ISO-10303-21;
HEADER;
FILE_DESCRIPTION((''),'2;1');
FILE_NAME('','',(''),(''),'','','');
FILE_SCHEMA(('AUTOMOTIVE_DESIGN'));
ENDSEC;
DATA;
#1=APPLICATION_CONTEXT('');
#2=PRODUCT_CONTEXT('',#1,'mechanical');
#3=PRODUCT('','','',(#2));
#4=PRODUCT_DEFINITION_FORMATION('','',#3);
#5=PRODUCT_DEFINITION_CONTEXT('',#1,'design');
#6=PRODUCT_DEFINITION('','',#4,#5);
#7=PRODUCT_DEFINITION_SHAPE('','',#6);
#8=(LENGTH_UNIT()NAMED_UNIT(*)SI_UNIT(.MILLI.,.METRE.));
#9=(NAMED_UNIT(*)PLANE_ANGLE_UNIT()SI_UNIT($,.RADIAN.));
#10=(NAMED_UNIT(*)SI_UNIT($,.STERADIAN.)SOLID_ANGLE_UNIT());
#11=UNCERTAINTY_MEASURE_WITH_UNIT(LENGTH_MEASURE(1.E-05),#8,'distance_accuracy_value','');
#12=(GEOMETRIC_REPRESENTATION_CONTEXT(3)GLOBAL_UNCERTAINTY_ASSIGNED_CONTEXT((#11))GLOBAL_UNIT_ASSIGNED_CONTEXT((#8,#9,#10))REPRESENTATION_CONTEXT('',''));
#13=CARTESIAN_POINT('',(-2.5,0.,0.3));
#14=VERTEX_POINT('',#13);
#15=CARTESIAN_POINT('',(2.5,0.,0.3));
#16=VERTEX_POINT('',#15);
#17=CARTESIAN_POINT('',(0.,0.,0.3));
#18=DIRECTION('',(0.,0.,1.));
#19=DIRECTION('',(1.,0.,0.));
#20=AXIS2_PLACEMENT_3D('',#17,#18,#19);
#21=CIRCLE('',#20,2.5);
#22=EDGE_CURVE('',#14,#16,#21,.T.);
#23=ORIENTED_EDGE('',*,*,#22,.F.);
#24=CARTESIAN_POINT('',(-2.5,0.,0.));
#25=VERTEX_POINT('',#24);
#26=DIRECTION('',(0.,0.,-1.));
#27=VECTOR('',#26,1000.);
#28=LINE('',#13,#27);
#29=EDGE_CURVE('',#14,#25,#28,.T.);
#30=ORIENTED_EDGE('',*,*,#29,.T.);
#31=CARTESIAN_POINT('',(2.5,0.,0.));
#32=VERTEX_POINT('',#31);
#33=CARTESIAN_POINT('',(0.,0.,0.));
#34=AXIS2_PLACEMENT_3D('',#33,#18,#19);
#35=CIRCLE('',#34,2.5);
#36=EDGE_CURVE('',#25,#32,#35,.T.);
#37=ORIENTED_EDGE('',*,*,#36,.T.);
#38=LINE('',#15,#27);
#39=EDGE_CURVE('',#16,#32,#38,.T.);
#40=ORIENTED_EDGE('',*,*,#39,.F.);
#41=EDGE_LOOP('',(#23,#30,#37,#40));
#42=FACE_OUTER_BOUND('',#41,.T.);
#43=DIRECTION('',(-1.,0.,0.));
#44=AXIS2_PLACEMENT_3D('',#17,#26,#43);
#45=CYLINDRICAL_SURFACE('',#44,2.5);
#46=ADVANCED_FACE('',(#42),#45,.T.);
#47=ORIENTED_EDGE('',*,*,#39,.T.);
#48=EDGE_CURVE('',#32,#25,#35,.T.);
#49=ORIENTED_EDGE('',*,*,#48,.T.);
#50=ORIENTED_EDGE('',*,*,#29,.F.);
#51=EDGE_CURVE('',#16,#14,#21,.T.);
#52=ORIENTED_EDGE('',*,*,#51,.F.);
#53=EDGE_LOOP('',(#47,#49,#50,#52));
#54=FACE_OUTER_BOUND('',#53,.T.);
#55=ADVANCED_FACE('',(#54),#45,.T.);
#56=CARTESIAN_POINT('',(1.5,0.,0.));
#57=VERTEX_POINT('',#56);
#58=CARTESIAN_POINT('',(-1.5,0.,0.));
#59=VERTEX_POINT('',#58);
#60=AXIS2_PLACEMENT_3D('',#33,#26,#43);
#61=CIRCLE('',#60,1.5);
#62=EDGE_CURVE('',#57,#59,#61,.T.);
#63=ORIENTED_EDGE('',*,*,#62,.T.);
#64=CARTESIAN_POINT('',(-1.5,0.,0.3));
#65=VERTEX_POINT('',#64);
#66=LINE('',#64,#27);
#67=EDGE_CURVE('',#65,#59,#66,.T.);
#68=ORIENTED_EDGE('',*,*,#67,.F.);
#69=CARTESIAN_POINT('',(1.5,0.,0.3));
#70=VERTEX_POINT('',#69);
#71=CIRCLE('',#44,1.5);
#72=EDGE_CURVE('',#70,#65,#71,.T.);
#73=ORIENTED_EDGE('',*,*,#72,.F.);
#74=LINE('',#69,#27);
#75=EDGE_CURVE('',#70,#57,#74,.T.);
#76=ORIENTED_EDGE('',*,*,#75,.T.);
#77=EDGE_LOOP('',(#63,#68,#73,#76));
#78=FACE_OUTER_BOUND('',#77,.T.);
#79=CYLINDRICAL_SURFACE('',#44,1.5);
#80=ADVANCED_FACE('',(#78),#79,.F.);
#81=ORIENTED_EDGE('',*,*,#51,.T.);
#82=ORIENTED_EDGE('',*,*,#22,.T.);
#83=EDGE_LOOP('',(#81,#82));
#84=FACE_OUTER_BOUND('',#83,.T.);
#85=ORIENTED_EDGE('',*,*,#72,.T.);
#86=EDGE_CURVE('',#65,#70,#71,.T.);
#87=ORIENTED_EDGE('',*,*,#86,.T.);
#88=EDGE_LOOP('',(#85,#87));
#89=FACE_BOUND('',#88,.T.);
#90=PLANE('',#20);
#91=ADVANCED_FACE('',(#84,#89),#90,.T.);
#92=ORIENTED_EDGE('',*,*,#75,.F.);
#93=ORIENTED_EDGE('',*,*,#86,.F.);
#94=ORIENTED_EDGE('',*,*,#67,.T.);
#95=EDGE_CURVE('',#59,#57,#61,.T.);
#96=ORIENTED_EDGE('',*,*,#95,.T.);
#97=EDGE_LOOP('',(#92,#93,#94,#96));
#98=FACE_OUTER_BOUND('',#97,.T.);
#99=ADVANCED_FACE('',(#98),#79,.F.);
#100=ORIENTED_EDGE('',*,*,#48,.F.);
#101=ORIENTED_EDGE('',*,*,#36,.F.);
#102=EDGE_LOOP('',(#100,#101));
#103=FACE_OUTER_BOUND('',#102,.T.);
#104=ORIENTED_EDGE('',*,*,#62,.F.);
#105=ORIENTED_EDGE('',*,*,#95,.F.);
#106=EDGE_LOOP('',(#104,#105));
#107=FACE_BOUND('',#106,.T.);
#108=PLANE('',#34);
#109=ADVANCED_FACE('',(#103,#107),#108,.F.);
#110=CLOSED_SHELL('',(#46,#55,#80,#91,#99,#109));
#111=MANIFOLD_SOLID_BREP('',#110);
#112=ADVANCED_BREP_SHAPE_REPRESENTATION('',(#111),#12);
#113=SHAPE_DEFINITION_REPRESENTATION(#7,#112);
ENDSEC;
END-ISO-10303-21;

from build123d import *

# Parameters (mm, degrees)
SKETCH_1_R           = 2.5
BOSS_EXTRUDE_1_DEPTH = 0.3
SKETCH_2_R           = 1.5
CUT_EXTRUDE_1_DEPTH  = 0.3


with BuildPart() as part:
    # Sketch 1 → Boss-Extrude 1 (new body)
    with BuildSketch(Plane.XY):
        Circle(SKETCH_1_R)
    extrude(amount=BOSS_EXTRUDE_1_DEPTH)

    # Sketch 2 → Cut-Extrude 1 (cut)
    with BuildSketch(Plane(origin=(0, 0, 0), x_dir=(-1, 0, 0), z_dir=(0, 0, -1))):
        Circle(SKETCH_2_R)
    extrude(amount=-CUT_EXTRUDE_1_DEPTH, mode=Mode.SUBTRACT)


solid = part.part
